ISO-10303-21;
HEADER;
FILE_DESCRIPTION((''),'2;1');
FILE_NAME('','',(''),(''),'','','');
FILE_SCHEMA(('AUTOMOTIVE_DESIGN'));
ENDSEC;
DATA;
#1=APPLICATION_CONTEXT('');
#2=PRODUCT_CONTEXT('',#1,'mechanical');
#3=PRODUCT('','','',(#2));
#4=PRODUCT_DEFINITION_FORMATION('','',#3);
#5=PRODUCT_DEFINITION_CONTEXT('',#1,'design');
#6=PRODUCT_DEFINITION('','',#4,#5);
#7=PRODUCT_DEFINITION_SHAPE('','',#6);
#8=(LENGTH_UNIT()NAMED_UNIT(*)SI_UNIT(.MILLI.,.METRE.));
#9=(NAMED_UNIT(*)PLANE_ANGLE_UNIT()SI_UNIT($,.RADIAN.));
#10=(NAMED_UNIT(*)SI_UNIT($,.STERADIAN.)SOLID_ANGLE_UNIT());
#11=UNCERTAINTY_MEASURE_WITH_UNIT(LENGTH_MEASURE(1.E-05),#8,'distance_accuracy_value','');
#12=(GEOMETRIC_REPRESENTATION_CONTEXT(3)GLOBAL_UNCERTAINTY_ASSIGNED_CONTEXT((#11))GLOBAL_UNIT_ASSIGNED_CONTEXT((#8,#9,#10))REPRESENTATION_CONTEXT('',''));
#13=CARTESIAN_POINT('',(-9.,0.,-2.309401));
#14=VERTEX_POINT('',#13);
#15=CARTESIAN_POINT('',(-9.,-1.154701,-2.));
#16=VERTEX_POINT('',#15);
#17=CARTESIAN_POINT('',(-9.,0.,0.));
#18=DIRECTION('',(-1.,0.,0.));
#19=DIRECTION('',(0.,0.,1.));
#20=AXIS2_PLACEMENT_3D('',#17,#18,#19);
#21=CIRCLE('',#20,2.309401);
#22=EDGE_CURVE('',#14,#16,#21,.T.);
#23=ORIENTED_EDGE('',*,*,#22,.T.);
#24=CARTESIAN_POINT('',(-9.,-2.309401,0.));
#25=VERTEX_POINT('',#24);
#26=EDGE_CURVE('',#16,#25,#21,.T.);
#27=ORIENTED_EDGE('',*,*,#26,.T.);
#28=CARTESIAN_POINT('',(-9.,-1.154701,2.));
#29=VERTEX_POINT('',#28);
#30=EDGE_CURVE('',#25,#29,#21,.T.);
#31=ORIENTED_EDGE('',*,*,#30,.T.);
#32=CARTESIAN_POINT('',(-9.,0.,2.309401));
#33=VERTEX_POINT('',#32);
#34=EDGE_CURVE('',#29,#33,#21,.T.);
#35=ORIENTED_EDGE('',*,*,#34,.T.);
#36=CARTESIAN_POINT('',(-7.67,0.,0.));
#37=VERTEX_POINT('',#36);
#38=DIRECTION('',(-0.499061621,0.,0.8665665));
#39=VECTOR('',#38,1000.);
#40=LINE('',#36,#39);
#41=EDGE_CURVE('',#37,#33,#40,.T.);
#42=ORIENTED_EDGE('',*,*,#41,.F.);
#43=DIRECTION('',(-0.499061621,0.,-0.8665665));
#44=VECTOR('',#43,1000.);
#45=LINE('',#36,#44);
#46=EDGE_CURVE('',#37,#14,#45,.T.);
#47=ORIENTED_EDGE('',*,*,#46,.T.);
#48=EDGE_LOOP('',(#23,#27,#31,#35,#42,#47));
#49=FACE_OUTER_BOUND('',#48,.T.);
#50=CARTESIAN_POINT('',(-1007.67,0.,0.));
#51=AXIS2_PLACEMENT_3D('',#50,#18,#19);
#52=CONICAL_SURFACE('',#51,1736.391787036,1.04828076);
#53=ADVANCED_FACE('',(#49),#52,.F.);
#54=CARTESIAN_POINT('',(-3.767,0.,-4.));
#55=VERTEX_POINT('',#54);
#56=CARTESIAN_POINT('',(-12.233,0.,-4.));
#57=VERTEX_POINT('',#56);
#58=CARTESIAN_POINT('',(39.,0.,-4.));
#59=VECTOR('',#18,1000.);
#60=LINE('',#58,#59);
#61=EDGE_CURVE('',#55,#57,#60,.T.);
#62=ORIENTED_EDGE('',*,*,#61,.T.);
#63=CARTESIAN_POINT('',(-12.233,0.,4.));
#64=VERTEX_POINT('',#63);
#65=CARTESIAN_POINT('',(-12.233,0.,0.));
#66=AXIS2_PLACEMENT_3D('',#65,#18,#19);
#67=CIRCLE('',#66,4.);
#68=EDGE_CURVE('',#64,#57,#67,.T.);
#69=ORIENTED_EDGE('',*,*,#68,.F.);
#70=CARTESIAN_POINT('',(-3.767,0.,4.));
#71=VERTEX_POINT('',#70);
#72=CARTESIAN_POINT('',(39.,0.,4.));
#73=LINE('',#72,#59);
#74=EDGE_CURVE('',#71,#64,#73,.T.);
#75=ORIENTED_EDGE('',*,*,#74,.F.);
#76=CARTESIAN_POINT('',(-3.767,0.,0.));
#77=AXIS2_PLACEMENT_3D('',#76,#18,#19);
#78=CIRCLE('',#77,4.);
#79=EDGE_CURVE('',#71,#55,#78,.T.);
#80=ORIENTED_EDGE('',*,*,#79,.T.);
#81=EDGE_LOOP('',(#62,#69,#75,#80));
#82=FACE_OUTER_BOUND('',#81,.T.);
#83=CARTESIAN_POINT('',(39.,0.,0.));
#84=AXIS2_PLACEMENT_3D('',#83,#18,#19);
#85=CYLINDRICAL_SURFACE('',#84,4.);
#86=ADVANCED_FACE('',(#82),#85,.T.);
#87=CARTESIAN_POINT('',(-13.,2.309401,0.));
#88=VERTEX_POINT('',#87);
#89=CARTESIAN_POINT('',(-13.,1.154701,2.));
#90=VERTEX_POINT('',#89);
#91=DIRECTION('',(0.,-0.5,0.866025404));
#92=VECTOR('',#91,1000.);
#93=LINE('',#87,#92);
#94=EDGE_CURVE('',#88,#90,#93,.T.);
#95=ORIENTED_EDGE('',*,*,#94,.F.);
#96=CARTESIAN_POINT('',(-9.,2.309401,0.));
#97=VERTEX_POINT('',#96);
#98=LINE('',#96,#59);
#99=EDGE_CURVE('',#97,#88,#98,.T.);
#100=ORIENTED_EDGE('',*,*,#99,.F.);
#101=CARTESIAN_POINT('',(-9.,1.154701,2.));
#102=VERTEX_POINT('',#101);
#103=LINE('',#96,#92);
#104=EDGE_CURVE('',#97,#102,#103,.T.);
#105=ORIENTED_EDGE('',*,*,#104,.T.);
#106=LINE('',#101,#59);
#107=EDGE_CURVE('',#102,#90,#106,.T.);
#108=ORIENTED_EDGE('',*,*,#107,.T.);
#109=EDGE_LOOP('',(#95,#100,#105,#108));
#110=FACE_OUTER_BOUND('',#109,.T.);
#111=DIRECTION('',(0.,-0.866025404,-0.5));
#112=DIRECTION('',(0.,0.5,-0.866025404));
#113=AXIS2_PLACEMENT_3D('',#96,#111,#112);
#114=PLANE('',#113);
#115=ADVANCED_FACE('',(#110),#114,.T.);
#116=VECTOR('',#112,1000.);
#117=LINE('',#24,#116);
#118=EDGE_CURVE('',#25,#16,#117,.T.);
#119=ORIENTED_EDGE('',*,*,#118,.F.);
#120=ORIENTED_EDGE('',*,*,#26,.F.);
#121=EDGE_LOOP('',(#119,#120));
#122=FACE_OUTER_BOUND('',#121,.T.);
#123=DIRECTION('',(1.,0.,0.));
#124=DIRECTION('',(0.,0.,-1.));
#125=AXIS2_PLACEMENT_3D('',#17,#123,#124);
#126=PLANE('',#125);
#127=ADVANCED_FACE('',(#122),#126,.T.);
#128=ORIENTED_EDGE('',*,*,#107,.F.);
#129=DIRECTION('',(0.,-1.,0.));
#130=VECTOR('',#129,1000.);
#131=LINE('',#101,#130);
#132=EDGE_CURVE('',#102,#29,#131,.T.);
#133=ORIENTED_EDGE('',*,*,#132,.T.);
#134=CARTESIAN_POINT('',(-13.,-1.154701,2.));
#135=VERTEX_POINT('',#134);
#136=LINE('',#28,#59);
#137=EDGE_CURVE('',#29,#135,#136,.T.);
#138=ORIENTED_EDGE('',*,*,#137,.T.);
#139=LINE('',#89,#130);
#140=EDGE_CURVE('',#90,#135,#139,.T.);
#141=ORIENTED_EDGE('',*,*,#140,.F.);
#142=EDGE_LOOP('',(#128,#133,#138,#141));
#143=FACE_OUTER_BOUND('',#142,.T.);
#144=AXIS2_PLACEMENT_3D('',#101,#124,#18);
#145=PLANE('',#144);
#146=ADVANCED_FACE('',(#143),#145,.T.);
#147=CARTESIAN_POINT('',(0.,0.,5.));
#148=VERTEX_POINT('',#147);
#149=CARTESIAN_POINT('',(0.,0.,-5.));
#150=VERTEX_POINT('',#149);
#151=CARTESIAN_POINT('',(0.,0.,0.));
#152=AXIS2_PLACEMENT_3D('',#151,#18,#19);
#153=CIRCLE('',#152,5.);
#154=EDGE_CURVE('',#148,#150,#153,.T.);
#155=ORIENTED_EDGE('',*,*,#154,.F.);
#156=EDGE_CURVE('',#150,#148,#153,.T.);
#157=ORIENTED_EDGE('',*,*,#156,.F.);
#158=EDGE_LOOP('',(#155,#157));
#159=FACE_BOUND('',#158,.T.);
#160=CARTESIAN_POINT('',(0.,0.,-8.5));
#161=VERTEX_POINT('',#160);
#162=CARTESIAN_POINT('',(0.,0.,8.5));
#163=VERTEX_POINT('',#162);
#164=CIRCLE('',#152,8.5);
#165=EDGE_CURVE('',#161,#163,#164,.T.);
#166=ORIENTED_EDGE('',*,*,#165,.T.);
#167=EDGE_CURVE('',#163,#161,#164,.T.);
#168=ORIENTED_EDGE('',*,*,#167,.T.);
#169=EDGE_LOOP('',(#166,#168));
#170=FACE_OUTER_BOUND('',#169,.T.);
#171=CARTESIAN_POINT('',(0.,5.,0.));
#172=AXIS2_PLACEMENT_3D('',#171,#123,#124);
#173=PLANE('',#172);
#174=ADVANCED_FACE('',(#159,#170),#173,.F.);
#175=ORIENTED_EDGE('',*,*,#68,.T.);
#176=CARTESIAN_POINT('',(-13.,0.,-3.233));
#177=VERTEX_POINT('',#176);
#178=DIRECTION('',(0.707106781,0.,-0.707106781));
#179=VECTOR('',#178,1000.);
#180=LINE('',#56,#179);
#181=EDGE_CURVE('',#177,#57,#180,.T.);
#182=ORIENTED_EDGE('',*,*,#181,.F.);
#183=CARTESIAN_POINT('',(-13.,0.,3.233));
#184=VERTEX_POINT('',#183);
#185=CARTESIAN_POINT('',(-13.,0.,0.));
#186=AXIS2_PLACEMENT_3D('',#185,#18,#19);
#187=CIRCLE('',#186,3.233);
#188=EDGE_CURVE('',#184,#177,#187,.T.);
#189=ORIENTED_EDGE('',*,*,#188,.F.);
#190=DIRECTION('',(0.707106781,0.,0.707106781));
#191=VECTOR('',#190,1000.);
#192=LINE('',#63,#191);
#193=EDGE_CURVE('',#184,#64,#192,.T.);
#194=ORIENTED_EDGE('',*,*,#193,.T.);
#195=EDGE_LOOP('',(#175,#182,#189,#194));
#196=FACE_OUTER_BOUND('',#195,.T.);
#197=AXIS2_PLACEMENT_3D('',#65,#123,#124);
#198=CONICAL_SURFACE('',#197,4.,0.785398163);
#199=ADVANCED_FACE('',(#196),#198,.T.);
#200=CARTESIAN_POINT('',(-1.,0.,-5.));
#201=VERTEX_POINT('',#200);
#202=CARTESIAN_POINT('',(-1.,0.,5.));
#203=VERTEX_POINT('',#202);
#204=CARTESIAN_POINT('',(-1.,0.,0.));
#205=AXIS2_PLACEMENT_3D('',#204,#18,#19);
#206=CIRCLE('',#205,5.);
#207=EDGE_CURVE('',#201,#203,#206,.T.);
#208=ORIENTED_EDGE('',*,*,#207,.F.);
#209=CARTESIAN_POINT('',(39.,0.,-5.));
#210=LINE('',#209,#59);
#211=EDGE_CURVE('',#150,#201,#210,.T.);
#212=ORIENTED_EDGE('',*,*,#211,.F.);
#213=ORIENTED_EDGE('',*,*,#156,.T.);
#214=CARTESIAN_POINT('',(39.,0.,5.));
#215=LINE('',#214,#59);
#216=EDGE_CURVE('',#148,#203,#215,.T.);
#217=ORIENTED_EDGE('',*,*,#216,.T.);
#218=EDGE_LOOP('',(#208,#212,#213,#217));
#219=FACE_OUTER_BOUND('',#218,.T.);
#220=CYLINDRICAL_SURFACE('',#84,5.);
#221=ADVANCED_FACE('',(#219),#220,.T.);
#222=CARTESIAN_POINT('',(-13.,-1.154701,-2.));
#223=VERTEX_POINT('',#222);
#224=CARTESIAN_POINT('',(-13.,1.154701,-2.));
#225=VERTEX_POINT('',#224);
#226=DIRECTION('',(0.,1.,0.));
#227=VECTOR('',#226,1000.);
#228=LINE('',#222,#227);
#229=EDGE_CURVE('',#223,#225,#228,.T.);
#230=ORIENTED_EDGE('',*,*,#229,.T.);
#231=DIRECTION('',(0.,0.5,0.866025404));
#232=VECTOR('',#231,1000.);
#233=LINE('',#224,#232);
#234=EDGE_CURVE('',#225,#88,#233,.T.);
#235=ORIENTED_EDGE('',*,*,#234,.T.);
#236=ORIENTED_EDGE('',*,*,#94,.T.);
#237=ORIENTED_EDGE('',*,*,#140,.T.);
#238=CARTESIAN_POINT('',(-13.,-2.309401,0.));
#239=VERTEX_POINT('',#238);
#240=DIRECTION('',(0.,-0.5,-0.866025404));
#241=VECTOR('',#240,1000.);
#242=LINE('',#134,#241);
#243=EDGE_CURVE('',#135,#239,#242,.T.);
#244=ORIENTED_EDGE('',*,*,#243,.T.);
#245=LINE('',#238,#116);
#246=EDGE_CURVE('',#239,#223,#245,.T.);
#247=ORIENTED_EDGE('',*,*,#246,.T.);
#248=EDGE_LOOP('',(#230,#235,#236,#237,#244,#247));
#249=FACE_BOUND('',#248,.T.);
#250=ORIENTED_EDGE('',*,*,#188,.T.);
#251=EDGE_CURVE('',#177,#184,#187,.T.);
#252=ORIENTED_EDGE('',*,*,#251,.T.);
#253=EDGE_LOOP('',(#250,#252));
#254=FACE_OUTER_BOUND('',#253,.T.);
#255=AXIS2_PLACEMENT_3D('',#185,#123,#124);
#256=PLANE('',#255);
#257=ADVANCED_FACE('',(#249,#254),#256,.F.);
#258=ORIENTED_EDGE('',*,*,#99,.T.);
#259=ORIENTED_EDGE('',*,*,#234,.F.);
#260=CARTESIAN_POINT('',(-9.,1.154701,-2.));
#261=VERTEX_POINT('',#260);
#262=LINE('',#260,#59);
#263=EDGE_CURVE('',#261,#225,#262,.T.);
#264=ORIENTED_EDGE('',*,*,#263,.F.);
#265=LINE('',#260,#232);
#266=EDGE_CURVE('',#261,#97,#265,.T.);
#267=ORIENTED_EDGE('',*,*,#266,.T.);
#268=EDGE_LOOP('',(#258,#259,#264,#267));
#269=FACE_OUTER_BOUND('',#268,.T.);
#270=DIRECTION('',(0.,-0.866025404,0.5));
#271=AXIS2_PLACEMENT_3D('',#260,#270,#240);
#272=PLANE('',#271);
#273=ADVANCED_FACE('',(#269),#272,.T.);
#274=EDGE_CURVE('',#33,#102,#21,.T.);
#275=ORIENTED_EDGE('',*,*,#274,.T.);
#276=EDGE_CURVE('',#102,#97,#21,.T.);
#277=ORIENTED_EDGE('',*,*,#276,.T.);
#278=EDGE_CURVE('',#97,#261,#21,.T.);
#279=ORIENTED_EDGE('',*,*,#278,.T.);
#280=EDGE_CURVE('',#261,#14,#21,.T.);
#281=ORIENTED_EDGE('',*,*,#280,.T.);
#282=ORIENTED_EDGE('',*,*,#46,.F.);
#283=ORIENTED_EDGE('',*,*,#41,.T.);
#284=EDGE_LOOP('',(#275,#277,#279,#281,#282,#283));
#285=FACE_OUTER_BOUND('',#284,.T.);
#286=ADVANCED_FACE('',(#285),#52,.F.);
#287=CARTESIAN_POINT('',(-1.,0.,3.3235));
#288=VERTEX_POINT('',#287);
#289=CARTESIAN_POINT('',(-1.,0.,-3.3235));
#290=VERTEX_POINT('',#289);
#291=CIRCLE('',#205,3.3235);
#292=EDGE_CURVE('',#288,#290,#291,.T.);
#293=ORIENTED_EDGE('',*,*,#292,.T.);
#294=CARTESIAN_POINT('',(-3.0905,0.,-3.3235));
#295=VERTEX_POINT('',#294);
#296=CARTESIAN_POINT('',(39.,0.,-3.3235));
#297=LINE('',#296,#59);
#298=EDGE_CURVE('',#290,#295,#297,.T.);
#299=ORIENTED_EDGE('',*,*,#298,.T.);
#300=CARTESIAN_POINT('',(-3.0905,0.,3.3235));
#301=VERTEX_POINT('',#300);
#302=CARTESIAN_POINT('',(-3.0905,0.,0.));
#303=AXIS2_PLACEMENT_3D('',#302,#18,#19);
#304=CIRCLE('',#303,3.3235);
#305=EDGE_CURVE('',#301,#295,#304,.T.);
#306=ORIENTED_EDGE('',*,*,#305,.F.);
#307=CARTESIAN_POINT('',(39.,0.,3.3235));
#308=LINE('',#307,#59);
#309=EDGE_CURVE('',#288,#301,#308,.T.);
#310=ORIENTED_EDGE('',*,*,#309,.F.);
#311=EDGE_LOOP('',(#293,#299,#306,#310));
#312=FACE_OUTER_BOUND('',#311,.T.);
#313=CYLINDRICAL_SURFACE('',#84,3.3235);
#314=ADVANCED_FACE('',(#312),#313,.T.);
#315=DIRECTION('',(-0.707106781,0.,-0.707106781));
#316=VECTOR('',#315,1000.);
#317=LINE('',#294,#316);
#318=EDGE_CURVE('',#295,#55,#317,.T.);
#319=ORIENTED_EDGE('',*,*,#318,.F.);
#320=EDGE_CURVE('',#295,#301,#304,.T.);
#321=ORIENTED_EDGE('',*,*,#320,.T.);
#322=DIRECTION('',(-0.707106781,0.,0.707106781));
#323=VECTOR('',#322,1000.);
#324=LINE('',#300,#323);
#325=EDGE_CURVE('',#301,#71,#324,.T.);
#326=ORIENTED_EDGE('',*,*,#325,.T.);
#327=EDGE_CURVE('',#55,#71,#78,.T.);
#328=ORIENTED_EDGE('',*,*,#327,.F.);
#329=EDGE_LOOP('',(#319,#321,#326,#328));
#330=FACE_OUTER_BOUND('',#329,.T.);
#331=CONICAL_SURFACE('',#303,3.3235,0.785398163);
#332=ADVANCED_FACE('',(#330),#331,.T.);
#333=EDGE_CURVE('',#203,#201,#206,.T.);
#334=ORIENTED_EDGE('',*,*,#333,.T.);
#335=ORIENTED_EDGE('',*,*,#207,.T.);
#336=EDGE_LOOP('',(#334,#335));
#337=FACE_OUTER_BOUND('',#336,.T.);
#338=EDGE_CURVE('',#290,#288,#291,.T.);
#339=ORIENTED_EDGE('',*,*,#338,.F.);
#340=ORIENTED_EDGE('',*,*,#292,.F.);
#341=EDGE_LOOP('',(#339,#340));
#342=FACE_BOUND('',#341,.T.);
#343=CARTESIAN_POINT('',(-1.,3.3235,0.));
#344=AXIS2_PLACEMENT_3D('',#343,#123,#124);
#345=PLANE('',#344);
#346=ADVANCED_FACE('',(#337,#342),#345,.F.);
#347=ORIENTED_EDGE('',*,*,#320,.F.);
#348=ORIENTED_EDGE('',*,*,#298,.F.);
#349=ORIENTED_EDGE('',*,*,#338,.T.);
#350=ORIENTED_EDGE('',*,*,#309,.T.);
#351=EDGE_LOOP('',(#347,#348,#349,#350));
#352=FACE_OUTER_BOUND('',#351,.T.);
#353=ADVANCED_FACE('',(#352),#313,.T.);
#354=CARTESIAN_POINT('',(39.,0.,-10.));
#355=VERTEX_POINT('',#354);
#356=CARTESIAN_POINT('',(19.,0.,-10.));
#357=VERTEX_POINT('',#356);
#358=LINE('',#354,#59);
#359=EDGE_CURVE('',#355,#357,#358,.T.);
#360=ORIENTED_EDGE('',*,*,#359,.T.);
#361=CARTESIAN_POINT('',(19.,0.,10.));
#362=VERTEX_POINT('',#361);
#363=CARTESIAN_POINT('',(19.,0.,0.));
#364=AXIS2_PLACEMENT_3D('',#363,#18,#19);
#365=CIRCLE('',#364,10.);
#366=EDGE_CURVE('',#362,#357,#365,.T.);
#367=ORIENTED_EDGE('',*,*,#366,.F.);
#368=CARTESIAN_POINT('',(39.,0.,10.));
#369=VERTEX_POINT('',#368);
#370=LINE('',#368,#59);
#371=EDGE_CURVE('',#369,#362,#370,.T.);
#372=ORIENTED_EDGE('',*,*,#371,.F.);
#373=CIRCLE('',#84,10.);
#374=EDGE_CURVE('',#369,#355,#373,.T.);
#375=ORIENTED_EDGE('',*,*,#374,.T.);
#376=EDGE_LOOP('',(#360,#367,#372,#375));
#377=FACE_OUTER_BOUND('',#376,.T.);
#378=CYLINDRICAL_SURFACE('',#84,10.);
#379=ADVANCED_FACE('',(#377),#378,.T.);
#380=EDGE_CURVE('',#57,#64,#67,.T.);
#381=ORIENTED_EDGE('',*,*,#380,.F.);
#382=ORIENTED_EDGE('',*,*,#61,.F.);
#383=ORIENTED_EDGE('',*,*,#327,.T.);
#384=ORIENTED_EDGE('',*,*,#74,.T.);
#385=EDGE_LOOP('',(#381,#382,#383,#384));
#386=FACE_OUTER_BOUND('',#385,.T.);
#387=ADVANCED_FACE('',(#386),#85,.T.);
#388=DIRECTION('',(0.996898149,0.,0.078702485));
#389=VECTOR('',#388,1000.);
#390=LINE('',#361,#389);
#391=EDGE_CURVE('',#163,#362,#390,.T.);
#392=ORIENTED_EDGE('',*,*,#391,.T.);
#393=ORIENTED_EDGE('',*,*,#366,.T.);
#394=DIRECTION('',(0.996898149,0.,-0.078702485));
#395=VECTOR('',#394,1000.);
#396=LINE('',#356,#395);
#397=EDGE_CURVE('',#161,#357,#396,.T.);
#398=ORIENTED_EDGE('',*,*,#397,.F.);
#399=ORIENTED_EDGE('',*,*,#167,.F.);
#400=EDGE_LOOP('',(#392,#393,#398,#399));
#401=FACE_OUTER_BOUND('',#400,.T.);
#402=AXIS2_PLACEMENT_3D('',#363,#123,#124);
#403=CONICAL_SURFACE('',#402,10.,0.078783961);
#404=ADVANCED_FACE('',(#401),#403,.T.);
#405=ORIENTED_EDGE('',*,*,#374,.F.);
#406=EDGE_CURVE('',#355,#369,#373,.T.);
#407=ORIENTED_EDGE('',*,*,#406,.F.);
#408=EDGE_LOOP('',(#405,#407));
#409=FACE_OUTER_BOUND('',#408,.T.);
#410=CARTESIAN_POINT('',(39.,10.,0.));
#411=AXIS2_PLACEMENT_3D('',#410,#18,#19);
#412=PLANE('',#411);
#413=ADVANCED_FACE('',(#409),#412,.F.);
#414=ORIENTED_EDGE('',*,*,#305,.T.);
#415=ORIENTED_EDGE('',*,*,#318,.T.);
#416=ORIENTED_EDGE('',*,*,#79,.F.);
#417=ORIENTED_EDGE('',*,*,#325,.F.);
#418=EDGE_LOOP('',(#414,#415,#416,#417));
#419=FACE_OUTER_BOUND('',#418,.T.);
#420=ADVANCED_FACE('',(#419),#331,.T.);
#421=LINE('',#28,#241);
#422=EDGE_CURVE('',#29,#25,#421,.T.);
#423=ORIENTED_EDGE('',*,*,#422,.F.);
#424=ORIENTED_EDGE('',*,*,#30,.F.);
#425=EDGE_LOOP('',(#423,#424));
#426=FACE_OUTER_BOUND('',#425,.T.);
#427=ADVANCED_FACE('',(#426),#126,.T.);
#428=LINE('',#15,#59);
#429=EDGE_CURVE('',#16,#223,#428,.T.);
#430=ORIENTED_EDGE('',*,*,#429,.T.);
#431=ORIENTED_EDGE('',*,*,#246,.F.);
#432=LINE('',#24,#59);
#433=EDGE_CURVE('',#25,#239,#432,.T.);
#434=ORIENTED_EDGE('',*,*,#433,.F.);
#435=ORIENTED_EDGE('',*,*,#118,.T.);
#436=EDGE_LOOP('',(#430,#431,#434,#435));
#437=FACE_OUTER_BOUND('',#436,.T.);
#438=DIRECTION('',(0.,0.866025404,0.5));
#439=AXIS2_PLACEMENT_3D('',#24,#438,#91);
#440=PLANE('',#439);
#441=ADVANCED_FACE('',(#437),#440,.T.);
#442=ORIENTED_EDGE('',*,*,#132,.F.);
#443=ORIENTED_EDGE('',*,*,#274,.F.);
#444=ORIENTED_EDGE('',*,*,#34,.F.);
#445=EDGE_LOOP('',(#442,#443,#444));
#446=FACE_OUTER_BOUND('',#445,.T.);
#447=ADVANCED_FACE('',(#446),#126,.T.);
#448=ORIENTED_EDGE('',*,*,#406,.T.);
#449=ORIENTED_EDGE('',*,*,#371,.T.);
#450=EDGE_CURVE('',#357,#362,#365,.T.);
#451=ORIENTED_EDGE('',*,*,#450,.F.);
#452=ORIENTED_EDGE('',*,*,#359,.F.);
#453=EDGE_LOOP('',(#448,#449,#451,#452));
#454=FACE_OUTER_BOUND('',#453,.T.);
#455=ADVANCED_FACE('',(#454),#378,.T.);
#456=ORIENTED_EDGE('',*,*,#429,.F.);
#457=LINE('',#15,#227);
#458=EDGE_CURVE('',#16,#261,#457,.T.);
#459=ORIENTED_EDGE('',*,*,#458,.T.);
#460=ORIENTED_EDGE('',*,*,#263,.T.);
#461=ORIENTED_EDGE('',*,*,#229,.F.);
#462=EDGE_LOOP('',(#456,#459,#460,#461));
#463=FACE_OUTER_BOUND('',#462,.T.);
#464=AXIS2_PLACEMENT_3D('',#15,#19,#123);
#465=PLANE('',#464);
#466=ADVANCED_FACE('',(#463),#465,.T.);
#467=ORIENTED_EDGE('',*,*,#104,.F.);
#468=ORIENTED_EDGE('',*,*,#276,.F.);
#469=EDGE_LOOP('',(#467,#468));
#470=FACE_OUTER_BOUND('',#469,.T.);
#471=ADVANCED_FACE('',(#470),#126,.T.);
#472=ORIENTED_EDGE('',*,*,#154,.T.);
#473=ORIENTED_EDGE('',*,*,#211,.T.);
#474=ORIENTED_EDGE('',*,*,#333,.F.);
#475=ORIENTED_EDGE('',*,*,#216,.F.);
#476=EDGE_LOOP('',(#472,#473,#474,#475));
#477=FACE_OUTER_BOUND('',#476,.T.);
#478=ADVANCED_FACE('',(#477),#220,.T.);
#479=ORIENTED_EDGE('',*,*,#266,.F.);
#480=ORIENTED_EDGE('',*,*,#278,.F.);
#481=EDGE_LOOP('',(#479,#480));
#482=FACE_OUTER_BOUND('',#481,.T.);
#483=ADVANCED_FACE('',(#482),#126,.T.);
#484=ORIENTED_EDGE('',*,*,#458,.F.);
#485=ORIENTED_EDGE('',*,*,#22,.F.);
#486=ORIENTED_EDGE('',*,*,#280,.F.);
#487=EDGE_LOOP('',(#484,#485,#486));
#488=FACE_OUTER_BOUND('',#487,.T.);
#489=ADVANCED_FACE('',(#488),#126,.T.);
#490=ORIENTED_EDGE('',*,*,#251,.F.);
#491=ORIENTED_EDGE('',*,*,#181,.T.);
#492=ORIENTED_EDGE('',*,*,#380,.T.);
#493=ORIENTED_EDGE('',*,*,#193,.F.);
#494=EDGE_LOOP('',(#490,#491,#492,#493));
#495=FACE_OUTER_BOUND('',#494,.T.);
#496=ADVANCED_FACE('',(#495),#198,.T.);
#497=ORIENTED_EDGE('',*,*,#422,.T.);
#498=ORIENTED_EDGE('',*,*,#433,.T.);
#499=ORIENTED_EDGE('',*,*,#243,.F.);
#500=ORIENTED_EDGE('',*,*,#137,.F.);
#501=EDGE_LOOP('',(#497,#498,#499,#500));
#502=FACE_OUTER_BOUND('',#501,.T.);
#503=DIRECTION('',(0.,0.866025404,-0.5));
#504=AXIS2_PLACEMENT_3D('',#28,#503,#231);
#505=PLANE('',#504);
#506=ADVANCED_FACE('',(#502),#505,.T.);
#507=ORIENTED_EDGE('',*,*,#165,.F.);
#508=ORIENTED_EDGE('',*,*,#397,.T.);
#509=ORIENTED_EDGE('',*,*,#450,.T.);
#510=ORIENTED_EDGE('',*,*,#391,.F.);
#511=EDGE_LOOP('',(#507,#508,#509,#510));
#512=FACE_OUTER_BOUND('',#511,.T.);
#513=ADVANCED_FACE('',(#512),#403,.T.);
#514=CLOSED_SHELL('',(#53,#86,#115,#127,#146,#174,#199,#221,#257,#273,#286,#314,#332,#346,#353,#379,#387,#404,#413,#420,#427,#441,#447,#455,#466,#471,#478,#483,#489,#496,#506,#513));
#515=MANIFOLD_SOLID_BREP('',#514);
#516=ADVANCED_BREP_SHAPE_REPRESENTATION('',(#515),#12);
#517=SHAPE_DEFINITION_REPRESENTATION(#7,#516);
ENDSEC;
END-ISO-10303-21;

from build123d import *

# Parameters (mm, degrees)
CUT_EXTRUDE1_DEPTH = 4


with BuildPart() as part:
    # Sketch1 → Revolve1 (revolve)
    with BuildSketch(Plane.XY, mode=Mode.PRIVATE) as revolve1_sk:
        Polygon((-13, 0), (-13, 3.233), (-12.233, 4), (-3.767, 4), (-3.0905, 3.3235), (-1, 3.3235), (-1, 5), (0, 5), (0, 8.5), (19, 10), (39, 10), (39, 0), align=None)
    revolve(revolve1_sk.sketch.rotate(Axis((39, 0, 0), (-1, 0, 0)), 270), axis=Axis((39, 0, 0), (-1, 0, 0)))

    # Sketch2 → Cut-Extrude1 (cut)
    with BuildSketch(Plane(origin=(-13, 0, 0), x_dir=(0, 0, -1), z_dir=(1, 0, 0))):
        Polygon((-2, 1.154700538), (-2, -1.154700538), (0, -2.309401077), (2, -1.154700538), (2, 1.154700538), (0, 2.309401077), align=None)
    extrude(amount=CUT_EXTRUDE1_DEPTH, mode=Mode.SUBTRACT)

    # Sketch3 → Cut-Revolve1 (revolve, cut)
    with BuildSketch(Plane.XY, mode=Mode.PRIVATE) as cut_revolve1_sk:
        Polygon((-9, 0), (-9, 2.309401077), (-7.67, 0), align=None)
    revolve(cut_revolve1_sk.sketch.rotate(Axis((-7.67, 0, 0), (-1, 0, 0)), 270), axis=Axis((-7.67, 0, 0), (-1, 0, 0)), mode=Mode.SUBTRACT)


solid = part.part
